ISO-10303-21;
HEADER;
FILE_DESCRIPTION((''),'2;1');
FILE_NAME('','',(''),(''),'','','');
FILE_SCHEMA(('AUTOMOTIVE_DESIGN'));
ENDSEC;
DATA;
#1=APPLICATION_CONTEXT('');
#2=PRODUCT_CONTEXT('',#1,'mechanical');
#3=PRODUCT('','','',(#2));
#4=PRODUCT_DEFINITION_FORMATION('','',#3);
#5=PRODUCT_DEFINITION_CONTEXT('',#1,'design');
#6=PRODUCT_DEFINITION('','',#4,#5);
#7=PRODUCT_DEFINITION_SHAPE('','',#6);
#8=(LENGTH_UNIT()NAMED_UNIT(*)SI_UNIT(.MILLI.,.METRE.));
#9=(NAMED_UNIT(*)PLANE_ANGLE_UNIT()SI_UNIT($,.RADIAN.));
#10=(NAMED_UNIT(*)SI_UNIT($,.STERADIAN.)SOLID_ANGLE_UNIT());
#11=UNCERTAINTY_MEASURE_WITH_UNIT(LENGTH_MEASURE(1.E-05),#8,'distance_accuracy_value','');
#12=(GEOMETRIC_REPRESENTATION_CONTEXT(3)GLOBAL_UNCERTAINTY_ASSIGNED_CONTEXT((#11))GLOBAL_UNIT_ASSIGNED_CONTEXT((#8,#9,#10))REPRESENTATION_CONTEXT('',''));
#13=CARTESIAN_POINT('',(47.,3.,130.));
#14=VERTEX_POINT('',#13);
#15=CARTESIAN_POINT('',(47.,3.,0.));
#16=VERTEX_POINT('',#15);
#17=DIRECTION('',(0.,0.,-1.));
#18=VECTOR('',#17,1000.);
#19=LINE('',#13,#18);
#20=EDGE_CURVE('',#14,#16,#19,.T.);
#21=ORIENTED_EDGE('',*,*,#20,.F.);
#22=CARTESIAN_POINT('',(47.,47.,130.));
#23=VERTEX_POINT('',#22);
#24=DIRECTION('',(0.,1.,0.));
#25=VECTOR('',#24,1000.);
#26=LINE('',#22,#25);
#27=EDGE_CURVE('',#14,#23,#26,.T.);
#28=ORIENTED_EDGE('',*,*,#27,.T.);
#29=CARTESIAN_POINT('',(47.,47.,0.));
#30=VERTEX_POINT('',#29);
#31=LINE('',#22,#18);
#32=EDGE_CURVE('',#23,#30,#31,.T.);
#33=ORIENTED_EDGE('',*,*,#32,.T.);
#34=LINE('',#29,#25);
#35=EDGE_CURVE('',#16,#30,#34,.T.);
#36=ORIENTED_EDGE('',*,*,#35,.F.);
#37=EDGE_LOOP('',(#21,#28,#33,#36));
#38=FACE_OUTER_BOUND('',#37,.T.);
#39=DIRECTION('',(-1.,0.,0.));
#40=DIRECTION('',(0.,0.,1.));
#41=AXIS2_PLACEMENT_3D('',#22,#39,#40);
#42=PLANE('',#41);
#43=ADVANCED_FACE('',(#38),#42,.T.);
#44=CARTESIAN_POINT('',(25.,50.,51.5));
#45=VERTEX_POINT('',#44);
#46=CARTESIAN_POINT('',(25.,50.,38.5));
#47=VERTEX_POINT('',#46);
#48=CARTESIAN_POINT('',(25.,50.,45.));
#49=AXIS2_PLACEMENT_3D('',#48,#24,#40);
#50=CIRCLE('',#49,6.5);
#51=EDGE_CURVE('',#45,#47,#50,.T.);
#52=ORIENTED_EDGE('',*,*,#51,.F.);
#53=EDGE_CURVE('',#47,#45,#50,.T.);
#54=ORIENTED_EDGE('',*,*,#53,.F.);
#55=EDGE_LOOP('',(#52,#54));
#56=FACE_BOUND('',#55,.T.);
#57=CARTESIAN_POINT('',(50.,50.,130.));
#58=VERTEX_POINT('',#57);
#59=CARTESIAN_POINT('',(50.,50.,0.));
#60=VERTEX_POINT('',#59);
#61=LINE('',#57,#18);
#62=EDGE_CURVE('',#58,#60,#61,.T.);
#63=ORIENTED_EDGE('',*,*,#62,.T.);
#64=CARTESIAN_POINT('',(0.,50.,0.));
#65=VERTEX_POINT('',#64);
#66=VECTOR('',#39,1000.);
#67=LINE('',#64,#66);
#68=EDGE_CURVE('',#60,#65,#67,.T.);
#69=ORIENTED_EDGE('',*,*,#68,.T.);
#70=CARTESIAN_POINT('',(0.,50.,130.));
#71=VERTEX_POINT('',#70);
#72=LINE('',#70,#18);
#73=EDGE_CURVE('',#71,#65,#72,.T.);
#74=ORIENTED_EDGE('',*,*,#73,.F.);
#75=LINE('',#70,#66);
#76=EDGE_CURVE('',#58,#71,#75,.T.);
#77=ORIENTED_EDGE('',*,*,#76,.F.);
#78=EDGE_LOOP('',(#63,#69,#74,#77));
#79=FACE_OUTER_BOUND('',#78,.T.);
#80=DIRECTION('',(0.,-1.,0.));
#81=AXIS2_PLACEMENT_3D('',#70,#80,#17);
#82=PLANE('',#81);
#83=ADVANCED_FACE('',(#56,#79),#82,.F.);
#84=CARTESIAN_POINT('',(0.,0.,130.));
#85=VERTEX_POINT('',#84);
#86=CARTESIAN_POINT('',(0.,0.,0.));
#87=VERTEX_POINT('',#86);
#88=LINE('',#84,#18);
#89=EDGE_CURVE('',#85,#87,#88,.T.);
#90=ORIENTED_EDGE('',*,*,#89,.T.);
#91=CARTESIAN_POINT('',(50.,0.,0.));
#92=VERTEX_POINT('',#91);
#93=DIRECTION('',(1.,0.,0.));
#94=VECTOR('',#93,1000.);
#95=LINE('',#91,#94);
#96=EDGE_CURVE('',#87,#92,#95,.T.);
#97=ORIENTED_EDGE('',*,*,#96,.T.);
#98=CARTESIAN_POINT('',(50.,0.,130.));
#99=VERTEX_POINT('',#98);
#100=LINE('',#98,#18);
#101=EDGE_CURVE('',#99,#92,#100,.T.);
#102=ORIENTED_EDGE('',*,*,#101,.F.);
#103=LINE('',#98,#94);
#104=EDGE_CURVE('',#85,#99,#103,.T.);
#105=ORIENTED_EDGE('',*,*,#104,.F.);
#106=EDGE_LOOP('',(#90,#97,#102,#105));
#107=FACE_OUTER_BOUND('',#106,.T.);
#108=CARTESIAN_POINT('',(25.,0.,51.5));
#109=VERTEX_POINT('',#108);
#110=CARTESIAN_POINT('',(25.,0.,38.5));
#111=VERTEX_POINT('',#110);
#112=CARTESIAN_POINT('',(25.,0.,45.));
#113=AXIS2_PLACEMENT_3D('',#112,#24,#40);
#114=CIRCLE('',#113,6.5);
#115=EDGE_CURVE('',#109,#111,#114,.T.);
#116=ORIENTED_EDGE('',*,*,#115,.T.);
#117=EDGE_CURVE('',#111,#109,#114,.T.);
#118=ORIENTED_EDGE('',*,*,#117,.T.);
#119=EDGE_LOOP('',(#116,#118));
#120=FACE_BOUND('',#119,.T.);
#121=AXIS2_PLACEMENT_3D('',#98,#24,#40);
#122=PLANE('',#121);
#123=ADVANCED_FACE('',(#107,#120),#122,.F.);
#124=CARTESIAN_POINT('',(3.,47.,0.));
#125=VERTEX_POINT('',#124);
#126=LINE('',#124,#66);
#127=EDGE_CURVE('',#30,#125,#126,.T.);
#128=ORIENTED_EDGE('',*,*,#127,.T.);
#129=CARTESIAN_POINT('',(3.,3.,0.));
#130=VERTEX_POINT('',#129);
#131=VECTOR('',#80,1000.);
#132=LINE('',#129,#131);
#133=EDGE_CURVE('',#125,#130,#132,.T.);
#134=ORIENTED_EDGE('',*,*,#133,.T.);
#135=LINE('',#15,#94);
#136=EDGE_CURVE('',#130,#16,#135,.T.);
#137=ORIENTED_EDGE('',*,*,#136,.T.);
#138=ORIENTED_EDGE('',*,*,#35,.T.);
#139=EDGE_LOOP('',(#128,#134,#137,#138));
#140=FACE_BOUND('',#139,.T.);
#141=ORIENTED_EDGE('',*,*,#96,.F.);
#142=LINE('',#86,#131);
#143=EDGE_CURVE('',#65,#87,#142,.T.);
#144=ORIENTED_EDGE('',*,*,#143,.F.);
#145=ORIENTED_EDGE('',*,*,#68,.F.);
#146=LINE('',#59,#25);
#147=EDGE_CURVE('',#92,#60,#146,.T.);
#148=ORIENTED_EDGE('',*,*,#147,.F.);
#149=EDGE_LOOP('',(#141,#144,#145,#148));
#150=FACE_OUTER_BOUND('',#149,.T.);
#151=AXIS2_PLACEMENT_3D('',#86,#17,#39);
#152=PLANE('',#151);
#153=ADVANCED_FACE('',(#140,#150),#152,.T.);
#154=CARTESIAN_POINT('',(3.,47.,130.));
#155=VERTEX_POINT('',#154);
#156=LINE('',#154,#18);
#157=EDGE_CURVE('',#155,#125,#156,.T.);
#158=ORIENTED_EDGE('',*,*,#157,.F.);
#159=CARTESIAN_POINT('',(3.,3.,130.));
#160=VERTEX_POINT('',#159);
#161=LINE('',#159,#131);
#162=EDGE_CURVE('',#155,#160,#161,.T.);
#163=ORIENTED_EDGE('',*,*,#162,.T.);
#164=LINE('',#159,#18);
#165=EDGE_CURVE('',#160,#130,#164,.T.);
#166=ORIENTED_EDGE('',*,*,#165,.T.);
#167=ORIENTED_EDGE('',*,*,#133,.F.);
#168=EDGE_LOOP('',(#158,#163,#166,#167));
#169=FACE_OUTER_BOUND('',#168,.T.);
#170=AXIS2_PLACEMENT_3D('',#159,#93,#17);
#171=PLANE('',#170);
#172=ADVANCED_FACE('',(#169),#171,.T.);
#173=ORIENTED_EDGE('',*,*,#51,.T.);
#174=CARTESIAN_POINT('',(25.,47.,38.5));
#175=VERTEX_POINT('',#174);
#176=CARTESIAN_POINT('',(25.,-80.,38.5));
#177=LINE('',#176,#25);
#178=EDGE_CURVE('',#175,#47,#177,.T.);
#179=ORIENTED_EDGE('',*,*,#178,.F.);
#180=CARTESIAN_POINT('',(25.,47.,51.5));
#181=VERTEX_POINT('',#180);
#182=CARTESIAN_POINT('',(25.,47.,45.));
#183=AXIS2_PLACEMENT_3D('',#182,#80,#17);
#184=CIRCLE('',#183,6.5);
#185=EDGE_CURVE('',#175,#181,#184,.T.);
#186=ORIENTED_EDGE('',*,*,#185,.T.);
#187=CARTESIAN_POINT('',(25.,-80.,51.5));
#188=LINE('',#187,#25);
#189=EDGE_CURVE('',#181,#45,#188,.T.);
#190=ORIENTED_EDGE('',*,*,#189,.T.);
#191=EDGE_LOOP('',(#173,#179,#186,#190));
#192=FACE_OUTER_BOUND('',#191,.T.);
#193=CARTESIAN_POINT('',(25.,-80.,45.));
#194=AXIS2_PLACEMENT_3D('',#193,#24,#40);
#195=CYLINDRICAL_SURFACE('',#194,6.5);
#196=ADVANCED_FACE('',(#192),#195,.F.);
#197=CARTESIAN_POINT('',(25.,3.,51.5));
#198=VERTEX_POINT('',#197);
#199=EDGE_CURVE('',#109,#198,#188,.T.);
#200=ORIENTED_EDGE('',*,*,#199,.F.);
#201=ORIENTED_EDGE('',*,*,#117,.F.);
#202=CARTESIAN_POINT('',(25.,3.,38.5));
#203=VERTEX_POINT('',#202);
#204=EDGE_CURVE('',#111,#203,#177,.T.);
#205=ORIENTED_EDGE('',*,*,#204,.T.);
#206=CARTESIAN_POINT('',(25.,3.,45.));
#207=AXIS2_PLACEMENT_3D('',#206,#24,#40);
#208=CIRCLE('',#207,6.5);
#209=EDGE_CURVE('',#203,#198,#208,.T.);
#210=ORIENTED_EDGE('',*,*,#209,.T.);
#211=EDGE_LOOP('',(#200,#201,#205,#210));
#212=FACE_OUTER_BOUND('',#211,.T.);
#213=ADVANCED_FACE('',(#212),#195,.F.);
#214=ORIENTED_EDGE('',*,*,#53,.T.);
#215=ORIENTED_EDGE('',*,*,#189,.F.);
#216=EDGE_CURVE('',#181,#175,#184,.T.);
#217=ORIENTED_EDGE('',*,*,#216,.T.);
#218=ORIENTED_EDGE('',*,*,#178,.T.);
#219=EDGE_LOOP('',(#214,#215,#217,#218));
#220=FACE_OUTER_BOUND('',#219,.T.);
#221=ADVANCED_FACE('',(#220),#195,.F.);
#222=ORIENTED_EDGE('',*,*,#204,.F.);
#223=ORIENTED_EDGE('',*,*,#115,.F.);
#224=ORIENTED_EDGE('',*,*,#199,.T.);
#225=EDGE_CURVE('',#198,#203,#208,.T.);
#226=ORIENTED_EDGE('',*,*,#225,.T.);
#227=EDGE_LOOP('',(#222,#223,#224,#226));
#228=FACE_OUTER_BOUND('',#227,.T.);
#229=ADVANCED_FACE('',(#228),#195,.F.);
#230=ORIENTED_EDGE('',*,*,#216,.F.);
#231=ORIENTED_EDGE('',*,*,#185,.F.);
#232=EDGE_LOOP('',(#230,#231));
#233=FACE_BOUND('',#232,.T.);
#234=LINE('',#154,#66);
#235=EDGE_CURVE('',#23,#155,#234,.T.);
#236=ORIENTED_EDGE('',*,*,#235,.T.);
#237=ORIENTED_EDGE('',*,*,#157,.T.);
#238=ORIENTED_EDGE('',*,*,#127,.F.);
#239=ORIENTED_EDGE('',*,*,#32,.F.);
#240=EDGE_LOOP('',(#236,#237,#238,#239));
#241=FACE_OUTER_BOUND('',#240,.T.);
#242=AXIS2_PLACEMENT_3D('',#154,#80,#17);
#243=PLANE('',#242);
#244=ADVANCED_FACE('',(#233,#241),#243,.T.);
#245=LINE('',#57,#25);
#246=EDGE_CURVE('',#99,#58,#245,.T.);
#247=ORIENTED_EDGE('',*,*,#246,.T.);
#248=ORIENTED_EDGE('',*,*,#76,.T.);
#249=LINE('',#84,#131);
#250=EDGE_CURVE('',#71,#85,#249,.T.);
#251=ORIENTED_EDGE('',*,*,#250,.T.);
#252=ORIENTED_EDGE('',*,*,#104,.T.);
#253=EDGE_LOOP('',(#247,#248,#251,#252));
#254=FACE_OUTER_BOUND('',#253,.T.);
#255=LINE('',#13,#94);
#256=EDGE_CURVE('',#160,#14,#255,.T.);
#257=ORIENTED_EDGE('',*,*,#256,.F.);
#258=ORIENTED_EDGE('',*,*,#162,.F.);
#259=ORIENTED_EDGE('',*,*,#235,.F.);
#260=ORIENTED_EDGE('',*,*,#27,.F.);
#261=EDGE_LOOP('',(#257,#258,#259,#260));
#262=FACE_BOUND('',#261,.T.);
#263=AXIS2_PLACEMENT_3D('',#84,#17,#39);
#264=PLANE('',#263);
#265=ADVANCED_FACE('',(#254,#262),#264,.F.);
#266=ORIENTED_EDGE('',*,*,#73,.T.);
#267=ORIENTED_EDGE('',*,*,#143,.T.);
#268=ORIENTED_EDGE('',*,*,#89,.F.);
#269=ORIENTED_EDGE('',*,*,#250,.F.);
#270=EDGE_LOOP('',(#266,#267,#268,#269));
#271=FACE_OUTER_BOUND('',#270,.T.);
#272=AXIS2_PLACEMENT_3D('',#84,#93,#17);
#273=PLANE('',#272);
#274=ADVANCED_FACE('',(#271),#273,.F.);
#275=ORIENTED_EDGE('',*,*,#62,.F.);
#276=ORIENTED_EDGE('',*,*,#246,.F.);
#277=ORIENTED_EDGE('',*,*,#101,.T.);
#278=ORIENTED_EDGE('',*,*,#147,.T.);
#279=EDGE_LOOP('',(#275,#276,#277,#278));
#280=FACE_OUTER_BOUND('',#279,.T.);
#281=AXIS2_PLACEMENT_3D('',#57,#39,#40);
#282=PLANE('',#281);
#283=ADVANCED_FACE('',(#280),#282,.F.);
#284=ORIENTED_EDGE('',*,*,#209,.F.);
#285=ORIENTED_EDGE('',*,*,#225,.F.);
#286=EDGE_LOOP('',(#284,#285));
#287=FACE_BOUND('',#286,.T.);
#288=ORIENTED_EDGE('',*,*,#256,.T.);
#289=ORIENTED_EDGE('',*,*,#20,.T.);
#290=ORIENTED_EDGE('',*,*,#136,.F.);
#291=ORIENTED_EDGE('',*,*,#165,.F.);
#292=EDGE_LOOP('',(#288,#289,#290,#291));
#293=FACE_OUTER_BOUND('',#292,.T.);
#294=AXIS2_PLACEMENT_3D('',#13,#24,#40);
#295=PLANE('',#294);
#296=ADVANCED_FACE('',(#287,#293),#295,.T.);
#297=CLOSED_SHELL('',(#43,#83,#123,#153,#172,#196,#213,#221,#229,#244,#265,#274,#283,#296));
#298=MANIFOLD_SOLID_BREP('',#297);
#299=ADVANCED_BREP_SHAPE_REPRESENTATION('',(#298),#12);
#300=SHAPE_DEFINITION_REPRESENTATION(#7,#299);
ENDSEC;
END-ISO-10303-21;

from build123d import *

# Parameters (mm, degrees)
SKETCH_1_W          = 50
SKETCH_1_H          = 50
SKETCH_1_W_2        = 44
SKETCH_1_H_2        = 44
EXTRUDE_1_DEPTH     = 130
SKETCH_5_R          = 6.5
CUT_EXTRUDE_1_DEPTH = 130


with BuildPart() as part:
    # 草图1 → 凸台-拉伸1 (new body)
    with BuildSketch(Plane.XY):
        with Locations((25, 25)):
            Rectangle(SKETCH_1_W, SKETCH_1_H)
        with Locations((25, 25)):
            Rectangle(SKETCH_1_W_2, SKETCH_1_H_2, mode=Mode.SUBTRACT)
    extrude(amount=EXTRUDE_1_DEPTH)

    # 草图5 → 切除-拉伸1 (cut)
    with BuildSketch(Plane(origin=(0, 50, 0), x_dir=(1, 0, 0), z_dir=(0, 1, 0))):
        with Locations(Location((25, -45, 0), (0, 0, 270))):
            Circle(SKETCH_5_R)
    extrude(amount=-CUT_EXTRUDE_1_DEPTH, mode=Mode.SUBTRACT)


solid = part.part
